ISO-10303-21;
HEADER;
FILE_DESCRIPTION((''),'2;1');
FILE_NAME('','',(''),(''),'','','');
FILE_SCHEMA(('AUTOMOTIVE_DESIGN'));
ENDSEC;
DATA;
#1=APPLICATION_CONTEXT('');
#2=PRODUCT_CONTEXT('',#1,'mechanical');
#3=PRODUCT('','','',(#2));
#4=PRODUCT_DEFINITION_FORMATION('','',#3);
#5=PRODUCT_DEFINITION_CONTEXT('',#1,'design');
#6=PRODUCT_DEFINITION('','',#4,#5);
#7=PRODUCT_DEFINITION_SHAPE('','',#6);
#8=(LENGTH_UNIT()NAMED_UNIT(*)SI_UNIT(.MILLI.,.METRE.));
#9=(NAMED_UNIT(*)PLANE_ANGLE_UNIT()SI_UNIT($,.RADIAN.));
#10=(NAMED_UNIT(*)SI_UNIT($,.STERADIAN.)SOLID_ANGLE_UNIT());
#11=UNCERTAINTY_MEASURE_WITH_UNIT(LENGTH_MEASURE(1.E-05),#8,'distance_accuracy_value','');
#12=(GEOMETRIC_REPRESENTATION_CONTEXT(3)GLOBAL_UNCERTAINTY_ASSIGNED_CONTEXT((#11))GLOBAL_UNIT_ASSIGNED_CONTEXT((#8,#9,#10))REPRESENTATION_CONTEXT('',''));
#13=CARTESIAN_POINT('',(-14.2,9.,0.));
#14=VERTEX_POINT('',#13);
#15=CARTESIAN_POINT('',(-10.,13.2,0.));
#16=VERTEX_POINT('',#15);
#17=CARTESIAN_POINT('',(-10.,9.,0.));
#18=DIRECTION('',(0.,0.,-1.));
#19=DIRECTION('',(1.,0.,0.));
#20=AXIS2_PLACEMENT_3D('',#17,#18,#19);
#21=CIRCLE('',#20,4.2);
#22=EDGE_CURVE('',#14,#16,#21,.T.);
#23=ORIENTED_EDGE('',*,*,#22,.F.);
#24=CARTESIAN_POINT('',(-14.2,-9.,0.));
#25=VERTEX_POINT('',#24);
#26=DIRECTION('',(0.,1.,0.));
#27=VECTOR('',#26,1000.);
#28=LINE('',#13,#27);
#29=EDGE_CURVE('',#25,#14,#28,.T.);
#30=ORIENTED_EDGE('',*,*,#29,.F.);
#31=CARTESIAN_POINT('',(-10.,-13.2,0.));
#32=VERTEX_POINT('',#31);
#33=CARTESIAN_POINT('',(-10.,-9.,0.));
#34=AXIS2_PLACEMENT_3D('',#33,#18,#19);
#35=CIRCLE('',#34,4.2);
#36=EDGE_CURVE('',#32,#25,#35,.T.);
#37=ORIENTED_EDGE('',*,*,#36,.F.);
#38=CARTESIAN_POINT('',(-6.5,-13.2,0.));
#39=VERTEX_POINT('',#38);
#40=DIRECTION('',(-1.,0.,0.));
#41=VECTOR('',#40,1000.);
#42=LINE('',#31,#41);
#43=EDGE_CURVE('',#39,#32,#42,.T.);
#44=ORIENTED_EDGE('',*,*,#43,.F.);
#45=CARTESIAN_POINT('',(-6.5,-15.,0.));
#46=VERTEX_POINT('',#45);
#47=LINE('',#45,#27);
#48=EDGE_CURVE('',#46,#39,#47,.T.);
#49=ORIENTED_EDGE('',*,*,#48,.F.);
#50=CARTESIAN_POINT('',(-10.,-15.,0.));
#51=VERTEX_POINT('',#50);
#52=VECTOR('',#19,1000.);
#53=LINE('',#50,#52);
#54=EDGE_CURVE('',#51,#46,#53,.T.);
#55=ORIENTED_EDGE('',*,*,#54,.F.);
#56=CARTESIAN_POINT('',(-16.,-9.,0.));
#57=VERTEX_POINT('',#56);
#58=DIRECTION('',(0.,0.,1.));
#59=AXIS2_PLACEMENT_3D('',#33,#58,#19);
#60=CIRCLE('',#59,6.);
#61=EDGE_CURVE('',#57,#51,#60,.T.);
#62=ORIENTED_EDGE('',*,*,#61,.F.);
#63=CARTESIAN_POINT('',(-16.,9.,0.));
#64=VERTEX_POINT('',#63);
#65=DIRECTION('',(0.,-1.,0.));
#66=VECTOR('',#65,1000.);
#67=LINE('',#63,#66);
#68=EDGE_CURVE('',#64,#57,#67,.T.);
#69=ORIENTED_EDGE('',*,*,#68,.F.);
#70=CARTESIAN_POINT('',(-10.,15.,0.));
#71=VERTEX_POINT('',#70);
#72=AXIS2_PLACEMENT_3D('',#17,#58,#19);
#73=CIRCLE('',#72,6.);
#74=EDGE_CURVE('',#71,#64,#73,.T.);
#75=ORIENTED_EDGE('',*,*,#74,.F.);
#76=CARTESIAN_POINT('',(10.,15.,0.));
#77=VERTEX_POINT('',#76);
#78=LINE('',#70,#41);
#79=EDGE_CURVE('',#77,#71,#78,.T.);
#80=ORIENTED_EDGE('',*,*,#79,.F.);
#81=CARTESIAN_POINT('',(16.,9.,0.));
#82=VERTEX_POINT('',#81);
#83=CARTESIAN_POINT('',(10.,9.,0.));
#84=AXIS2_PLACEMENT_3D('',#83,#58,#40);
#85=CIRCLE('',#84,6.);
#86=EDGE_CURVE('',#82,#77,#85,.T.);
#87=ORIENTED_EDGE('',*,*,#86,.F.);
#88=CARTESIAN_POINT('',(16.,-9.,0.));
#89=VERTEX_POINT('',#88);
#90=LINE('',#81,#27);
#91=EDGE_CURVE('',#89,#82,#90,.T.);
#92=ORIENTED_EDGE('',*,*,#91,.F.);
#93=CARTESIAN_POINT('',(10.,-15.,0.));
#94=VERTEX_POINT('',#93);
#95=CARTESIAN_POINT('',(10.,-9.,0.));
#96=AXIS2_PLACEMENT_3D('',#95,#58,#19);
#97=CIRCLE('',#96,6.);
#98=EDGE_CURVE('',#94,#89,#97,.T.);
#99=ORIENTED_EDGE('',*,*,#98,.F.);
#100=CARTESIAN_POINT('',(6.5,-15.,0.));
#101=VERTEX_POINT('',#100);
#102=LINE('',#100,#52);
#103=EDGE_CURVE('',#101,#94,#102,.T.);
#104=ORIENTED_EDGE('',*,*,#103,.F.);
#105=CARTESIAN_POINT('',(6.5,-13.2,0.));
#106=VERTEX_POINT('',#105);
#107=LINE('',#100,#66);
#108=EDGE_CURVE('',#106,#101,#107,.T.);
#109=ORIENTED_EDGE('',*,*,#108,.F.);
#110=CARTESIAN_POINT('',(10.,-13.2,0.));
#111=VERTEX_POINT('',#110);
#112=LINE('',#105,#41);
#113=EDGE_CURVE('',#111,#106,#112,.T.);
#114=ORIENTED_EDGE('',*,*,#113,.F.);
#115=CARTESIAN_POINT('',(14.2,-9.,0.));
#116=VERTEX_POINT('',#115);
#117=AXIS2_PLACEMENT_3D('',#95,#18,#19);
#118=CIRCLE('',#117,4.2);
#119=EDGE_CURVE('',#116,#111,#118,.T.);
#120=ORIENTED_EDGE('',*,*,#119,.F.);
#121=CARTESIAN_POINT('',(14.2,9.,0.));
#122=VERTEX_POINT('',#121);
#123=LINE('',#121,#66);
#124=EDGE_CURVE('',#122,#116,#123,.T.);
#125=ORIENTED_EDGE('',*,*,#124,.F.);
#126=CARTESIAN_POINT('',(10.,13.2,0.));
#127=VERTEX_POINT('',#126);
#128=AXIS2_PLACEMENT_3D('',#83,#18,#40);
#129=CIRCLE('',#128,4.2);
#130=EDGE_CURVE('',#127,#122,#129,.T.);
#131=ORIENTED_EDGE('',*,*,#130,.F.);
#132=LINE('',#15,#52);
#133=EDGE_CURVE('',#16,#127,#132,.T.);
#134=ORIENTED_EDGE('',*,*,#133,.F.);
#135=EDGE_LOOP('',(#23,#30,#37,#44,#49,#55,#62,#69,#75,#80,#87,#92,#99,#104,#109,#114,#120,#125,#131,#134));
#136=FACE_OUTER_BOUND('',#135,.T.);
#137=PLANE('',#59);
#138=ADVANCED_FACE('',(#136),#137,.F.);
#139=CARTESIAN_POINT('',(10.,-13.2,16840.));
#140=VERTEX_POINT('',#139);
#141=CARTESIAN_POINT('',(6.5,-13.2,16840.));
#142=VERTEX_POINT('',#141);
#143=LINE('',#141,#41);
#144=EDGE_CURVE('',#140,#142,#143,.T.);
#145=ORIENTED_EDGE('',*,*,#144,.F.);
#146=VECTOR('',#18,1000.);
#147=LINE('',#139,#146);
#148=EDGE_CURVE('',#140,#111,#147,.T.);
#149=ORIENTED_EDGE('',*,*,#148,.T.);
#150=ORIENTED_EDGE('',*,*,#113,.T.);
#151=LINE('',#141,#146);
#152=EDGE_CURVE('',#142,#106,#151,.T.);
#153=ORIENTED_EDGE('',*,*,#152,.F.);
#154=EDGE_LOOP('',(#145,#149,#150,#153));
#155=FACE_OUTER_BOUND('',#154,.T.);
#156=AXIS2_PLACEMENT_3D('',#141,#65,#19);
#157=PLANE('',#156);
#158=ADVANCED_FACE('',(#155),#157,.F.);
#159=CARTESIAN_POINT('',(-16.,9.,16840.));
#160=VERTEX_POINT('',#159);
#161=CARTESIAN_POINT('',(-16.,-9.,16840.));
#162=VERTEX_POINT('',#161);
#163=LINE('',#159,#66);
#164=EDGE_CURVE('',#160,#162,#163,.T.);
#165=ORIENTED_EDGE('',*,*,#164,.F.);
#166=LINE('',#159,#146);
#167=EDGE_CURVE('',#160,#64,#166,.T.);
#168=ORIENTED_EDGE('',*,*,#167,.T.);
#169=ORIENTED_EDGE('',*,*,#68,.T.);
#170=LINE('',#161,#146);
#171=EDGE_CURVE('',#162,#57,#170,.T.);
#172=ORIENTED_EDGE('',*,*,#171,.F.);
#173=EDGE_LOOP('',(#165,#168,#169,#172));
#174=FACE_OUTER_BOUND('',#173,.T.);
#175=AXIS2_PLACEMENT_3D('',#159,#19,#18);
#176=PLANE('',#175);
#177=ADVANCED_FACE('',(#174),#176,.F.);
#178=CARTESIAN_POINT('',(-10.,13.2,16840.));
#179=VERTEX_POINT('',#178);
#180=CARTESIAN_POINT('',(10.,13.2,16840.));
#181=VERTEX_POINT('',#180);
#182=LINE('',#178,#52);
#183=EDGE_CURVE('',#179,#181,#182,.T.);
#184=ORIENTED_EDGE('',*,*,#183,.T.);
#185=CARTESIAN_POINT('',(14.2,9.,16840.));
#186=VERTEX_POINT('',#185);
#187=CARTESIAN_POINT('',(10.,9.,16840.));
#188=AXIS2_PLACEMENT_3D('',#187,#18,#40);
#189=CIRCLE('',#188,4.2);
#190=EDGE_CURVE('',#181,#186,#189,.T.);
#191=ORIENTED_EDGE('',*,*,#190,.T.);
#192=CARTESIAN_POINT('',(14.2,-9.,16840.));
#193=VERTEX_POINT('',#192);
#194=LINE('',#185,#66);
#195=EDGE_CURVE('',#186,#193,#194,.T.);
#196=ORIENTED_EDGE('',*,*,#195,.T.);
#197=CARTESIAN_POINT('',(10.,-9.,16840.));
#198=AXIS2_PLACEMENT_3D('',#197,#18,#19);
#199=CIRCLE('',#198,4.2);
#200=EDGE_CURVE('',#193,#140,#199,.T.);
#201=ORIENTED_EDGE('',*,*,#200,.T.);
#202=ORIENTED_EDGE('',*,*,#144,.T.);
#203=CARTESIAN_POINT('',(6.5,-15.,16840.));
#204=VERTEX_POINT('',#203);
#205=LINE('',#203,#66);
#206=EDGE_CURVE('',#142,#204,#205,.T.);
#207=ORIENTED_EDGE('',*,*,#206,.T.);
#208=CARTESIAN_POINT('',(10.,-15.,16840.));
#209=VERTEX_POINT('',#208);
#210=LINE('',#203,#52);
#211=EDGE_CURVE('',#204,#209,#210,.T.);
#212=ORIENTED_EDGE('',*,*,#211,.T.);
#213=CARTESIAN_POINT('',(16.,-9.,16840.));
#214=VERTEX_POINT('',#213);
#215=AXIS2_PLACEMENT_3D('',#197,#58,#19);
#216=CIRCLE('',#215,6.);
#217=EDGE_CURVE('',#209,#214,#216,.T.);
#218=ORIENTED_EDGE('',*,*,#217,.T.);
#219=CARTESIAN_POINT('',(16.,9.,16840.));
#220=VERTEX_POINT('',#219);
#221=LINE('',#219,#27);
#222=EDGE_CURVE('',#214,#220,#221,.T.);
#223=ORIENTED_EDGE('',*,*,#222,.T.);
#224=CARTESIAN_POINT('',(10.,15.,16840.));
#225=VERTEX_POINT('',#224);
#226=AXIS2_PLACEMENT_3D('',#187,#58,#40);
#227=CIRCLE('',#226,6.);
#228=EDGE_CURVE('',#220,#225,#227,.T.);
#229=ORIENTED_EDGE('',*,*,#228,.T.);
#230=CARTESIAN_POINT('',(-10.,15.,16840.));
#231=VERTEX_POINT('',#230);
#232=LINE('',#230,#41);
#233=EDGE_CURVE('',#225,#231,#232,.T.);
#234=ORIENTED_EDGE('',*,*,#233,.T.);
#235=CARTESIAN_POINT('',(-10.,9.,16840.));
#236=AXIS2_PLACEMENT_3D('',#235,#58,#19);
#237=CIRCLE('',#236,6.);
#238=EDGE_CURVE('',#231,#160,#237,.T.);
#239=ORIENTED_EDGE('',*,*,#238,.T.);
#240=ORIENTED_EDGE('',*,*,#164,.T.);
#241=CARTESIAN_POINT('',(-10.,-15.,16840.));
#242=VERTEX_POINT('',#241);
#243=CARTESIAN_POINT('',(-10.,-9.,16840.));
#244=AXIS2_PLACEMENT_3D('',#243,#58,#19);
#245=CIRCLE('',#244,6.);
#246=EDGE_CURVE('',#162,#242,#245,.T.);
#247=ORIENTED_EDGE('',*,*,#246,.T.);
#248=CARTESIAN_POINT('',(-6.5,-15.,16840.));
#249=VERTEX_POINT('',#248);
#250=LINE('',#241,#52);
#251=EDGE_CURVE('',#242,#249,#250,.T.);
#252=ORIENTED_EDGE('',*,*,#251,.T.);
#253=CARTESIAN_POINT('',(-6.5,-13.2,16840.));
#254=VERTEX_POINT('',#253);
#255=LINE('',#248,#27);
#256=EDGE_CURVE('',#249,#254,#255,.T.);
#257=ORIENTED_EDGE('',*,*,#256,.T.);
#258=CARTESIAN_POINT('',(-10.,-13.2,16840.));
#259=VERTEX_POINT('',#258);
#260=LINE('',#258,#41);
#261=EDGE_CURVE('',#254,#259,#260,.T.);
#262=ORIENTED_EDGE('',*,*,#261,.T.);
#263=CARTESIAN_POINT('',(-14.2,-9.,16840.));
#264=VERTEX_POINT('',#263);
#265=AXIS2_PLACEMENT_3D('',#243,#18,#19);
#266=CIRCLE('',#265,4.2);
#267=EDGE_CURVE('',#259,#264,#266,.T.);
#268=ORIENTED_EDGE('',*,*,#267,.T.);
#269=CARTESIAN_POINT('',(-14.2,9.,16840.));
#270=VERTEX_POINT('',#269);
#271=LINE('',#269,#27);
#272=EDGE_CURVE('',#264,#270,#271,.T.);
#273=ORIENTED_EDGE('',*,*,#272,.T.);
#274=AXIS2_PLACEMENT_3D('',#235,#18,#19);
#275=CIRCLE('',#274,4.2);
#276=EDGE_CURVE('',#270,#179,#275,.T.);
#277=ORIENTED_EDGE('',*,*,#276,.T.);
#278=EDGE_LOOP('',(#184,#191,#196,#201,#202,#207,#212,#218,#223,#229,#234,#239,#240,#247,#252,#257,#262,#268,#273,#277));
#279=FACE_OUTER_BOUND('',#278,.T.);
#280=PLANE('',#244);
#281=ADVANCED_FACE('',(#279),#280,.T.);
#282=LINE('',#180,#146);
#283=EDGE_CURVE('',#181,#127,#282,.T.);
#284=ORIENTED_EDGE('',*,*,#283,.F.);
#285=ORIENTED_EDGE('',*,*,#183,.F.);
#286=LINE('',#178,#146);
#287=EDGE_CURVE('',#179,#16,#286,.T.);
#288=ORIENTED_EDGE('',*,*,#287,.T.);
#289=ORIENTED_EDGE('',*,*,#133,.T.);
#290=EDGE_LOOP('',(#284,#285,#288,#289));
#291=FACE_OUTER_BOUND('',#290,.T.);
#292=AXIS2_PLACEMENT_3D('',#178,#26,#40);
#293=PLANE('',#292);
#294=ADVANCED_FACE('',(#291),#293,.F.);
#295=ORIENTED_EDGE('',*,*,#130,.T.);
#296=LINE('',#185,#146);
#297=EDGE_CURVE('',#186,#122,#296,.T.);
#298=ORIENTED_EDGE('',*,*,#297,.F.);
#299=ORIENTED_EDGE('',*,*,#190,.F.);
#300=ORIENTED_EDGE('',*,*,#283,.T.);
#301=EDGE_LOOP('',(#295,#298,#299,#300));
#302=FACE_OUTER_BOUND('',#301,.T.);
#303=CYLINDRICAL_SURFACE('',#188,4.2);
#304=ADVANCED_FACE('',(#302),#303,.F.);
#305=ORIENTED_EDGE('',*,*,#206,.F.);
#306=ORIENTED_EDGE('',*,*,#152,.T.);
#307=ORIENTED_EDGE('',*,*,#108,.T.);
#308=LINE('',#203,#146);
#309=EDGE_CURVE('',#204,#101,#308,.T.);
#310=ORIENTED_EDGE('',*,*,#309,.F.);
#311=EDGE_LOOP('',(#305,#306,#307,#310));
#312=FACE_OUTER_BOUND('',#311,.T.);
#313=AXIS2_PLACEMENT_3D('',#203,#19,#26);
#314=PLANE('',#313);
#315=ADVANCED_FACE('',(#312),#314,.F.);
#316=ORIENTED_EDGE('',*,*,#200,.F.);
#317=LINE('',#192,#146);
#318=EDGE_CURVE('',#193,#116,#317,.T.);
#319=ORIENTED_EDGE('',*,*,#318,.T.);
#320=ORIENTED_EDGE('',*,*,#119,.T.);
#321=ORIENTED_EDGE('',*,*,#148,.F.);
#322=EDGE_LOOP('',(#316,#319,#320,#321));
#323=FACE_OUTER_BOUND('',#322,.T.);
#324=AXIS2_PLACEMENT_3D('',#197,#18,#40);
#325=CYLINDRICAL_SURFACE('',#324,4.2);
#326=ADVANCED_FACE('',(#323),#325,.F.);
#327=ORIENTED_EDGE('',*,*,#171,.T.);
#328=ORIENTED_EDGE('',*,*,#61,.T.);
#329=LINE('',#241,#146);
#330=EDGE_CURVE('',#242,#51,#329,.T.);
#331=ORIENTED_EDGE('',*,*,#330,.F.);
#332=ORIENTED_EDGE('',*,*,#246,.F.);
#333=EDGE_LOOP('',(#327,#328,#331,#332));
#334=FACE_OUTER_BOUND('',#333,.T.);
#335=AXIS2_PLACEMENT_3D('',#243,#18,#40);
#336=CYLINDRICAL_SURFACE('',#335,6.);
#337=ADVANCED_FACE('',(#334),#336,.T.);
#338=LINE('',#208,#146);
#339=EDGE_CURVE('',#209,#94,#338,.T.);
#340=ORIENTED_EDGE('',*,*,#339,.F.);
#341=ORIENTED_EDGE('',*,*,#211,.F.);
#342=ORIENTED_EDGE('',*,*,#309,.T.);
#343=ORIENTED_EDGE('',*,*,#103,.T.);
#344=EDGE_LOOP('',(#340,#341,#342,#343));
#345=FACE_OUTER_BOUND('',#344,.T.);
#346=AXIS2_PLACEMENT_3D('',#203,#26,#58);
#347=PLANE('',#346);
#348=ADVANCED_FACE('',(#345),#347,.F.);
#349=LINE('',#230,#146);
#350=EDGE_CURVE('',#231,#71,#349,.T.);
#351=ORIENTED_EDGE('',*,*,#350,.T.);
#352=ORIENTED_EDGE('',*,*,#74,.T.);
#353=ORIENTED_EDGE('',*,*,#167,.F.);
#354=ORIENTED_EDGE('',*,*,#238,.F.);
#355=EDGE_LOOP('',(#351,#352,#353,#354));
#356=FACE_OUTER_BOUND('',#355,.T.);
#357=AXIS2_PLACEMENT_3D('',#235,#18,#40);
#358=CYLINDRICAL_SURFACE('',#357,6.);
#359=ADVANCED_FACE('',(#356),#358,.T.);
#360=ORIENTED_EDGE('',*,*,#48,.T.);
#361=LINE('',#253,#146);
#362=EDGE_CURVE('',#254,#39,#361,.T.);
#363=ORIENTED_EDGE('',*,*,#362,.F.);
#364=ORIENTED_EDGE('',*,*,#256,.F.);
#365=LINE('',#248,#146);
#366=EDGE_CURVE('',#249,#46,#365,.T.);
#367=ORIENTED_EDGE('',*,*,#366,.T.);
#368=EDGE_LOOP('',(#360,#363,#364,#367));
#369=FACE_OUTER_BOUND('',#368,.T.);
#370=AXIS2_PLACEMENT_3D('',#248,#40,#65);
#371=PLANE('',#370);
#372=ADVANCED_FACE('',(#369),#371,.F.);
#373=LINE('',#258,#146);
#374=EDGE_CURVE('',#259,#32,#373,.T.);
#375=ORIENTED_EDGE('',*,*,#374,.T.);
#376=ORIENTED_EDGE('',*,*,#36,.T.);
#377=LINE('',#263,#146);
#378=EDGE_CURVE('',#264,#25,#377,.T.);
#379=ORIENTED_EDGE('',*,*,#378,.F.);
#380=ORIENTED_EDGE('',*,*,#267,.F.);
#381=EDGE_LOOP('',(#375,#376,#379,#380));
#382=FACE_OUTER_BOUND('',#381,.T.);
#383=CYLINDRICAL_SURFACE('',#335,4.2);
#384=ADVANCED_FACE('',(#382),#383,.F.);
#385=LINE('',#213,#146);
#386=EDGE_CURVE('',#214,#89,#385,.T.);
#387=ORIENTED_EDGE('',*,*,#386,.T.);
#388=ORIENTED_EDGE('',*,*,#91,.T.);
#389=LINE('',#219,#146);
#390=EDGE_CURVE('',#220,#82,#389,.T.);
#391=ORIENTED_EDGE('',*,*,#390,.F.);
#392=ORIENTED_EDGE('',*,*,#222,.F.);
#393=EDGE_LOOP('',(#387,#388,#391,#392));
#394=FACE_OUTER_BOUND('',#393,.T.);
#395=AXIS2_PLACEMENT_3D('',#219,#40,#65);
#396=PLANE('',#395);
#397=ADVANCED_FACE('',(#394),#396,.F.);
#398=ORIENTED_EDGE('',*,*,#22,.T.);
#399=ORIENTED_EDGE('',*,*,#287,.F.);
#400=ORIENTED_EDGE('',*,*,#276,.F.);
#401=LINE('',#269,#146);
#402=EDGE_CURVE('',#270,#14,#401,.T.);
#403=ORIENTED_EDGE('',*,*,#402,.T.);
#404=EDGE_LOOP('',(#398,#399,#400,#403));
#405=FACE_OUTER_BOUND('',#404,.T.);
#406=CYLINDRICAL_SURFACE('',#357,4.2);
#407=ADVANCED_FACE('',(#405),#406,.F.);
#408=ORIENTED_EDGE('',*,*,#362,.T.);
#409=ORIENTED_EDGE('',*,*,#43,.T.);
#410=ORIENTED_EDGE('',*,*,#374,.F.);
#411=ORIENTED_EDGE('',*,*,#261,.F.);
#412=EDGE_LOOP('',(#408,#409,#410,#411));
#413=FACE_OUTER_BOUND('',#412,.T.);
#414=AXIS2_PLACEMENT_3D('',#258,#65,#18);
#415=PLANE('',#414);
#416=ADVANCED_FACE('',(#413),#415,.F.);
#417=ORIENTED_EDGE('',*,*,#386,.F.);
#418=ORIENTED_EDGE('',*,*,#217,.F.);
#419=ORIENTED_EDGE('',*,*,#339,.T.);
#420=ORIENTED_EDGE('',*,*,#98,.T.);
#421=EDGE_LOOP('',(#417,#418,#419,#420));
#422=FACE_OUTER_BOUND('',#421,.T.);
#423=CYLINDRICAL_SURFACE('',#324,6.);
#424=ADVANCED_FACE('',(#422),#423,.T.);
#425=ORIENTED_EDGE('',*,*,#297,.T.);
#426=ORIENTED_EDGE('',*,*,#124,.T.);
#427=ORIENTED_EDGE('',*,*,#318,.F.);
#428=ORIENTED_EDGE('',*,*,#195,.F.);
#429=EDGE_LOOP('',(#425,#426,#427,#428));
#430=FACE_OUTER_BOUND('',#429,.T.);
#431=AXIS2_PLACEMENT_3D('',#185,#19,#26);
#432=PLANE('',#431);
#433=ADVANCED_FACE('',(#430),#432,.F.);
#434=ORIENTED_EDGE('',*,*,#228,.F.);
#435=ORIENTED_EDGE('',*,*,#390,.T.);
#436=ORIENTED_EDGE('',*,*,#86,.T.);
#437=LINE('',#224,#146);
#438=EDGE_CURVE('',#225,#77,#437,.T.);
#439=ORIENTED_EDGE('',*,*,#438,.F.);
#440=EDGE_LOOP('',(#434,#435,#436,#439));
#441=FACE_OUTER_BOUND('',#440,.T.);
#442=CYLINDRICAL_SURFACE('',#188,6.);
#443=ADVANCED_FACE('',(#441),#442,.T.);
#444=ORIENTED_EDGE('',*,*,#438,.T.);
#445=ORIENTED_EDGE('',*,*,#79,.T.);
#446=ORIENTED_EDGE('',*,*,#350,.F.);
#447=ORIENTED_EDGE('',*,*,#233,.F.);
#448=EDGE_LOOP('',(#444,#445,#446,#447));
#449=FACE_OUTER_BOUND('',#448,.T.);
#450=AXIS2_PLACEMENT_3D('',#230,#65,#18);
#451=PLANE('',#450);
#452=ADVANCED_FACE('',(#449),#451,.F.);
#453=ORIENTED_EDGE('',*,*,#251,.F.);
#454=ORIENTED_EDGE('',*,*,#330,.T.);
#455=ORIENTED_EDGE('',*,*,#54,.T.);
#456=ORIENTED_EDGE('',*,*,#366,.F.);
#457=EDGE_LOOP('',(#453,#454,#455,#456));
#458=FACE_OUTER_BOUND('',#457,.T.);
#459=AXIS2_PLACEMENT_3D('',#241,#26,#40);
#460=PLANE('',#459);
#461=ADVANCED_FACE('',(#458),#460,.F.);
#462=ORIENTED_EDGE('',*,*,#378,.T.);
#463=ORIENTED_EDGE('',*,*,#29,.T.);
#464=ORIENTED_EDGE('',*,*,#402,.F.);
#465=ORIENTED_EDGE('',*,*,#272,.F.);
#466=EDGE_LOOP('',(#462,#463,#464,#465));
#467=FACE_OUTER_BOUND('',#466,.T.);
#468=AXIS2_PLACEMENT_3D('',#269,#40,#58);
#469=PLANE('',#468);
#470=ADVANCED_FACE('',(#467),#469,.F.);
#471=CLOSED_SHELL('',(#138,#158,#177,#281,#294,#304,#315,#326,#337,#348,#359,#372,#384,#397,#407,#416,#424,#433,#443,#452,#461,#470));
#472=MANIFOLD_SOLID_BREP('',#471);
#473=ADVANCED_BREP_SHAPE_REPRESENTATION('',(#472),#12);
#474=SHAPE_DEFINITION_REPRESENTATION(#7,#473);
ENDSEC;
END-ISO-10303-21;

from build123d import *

# Parameters (mm, degrees)
BOSS_EXTRUDE1_DEPTH = 16840


with BuildPart() as part:
    # Sketch1 → Boss-Extrude1 (new body)
    with BuildSketch(Plane.XY):
        with BuildLine():
            Line((-10, -13.2), (-6.5, -13.2))
            Line((-6.5, -13.2), (-6.5, -15))
            Line((-6.5, -15), (-10, -15))
            ThreePointArc((-10, -15), (-14.242640687, -13.242640687), (-16, -9))
            Line((-16, -9), (-16, 9))
            ThreePointArc((-16, 9), (-14.242640687, 13.242640687), (-10, 15))
            Line((-10, 15), (10, 15))
            ThreePointArc((10, 15), (14.242640687, 13.242640687), (16, 9))
            Line((16, 9), (16, -9))
            ThreePointArc((16, -9), (14.242640687, -13.242640687), (10, -15))
            Line((10, -15), (6.5, -15))
            Line((6.5, -15), (6.5, -13.2))
            Line((6.5, -13.2), (10, -13.2))
            ThreePointArc((10, -13.2), (12.969848481, -11.969848481), (14.2, -9))
            Line((14.2, -9), (14.2, 9))
            ThreePointArc((14.2, 9), (12.969848481, 11.969848481), (10, 13.2))
            Line((10, 13.2), (-10, 13.2))
            ThreePointArc((-10, 13.2), (-12.969848481, 11.969848481), (-14.2, 9))
            Line((-14.2, 9), (-14.2, -9))
            ThreePointArc((-14.2, -9), (-12.969848481, -11.969848481), (-10, -13.2))
        make_face()
    extrude(amount=BOSS_EXTRUDE1_DEPTH)


solid = part.part
